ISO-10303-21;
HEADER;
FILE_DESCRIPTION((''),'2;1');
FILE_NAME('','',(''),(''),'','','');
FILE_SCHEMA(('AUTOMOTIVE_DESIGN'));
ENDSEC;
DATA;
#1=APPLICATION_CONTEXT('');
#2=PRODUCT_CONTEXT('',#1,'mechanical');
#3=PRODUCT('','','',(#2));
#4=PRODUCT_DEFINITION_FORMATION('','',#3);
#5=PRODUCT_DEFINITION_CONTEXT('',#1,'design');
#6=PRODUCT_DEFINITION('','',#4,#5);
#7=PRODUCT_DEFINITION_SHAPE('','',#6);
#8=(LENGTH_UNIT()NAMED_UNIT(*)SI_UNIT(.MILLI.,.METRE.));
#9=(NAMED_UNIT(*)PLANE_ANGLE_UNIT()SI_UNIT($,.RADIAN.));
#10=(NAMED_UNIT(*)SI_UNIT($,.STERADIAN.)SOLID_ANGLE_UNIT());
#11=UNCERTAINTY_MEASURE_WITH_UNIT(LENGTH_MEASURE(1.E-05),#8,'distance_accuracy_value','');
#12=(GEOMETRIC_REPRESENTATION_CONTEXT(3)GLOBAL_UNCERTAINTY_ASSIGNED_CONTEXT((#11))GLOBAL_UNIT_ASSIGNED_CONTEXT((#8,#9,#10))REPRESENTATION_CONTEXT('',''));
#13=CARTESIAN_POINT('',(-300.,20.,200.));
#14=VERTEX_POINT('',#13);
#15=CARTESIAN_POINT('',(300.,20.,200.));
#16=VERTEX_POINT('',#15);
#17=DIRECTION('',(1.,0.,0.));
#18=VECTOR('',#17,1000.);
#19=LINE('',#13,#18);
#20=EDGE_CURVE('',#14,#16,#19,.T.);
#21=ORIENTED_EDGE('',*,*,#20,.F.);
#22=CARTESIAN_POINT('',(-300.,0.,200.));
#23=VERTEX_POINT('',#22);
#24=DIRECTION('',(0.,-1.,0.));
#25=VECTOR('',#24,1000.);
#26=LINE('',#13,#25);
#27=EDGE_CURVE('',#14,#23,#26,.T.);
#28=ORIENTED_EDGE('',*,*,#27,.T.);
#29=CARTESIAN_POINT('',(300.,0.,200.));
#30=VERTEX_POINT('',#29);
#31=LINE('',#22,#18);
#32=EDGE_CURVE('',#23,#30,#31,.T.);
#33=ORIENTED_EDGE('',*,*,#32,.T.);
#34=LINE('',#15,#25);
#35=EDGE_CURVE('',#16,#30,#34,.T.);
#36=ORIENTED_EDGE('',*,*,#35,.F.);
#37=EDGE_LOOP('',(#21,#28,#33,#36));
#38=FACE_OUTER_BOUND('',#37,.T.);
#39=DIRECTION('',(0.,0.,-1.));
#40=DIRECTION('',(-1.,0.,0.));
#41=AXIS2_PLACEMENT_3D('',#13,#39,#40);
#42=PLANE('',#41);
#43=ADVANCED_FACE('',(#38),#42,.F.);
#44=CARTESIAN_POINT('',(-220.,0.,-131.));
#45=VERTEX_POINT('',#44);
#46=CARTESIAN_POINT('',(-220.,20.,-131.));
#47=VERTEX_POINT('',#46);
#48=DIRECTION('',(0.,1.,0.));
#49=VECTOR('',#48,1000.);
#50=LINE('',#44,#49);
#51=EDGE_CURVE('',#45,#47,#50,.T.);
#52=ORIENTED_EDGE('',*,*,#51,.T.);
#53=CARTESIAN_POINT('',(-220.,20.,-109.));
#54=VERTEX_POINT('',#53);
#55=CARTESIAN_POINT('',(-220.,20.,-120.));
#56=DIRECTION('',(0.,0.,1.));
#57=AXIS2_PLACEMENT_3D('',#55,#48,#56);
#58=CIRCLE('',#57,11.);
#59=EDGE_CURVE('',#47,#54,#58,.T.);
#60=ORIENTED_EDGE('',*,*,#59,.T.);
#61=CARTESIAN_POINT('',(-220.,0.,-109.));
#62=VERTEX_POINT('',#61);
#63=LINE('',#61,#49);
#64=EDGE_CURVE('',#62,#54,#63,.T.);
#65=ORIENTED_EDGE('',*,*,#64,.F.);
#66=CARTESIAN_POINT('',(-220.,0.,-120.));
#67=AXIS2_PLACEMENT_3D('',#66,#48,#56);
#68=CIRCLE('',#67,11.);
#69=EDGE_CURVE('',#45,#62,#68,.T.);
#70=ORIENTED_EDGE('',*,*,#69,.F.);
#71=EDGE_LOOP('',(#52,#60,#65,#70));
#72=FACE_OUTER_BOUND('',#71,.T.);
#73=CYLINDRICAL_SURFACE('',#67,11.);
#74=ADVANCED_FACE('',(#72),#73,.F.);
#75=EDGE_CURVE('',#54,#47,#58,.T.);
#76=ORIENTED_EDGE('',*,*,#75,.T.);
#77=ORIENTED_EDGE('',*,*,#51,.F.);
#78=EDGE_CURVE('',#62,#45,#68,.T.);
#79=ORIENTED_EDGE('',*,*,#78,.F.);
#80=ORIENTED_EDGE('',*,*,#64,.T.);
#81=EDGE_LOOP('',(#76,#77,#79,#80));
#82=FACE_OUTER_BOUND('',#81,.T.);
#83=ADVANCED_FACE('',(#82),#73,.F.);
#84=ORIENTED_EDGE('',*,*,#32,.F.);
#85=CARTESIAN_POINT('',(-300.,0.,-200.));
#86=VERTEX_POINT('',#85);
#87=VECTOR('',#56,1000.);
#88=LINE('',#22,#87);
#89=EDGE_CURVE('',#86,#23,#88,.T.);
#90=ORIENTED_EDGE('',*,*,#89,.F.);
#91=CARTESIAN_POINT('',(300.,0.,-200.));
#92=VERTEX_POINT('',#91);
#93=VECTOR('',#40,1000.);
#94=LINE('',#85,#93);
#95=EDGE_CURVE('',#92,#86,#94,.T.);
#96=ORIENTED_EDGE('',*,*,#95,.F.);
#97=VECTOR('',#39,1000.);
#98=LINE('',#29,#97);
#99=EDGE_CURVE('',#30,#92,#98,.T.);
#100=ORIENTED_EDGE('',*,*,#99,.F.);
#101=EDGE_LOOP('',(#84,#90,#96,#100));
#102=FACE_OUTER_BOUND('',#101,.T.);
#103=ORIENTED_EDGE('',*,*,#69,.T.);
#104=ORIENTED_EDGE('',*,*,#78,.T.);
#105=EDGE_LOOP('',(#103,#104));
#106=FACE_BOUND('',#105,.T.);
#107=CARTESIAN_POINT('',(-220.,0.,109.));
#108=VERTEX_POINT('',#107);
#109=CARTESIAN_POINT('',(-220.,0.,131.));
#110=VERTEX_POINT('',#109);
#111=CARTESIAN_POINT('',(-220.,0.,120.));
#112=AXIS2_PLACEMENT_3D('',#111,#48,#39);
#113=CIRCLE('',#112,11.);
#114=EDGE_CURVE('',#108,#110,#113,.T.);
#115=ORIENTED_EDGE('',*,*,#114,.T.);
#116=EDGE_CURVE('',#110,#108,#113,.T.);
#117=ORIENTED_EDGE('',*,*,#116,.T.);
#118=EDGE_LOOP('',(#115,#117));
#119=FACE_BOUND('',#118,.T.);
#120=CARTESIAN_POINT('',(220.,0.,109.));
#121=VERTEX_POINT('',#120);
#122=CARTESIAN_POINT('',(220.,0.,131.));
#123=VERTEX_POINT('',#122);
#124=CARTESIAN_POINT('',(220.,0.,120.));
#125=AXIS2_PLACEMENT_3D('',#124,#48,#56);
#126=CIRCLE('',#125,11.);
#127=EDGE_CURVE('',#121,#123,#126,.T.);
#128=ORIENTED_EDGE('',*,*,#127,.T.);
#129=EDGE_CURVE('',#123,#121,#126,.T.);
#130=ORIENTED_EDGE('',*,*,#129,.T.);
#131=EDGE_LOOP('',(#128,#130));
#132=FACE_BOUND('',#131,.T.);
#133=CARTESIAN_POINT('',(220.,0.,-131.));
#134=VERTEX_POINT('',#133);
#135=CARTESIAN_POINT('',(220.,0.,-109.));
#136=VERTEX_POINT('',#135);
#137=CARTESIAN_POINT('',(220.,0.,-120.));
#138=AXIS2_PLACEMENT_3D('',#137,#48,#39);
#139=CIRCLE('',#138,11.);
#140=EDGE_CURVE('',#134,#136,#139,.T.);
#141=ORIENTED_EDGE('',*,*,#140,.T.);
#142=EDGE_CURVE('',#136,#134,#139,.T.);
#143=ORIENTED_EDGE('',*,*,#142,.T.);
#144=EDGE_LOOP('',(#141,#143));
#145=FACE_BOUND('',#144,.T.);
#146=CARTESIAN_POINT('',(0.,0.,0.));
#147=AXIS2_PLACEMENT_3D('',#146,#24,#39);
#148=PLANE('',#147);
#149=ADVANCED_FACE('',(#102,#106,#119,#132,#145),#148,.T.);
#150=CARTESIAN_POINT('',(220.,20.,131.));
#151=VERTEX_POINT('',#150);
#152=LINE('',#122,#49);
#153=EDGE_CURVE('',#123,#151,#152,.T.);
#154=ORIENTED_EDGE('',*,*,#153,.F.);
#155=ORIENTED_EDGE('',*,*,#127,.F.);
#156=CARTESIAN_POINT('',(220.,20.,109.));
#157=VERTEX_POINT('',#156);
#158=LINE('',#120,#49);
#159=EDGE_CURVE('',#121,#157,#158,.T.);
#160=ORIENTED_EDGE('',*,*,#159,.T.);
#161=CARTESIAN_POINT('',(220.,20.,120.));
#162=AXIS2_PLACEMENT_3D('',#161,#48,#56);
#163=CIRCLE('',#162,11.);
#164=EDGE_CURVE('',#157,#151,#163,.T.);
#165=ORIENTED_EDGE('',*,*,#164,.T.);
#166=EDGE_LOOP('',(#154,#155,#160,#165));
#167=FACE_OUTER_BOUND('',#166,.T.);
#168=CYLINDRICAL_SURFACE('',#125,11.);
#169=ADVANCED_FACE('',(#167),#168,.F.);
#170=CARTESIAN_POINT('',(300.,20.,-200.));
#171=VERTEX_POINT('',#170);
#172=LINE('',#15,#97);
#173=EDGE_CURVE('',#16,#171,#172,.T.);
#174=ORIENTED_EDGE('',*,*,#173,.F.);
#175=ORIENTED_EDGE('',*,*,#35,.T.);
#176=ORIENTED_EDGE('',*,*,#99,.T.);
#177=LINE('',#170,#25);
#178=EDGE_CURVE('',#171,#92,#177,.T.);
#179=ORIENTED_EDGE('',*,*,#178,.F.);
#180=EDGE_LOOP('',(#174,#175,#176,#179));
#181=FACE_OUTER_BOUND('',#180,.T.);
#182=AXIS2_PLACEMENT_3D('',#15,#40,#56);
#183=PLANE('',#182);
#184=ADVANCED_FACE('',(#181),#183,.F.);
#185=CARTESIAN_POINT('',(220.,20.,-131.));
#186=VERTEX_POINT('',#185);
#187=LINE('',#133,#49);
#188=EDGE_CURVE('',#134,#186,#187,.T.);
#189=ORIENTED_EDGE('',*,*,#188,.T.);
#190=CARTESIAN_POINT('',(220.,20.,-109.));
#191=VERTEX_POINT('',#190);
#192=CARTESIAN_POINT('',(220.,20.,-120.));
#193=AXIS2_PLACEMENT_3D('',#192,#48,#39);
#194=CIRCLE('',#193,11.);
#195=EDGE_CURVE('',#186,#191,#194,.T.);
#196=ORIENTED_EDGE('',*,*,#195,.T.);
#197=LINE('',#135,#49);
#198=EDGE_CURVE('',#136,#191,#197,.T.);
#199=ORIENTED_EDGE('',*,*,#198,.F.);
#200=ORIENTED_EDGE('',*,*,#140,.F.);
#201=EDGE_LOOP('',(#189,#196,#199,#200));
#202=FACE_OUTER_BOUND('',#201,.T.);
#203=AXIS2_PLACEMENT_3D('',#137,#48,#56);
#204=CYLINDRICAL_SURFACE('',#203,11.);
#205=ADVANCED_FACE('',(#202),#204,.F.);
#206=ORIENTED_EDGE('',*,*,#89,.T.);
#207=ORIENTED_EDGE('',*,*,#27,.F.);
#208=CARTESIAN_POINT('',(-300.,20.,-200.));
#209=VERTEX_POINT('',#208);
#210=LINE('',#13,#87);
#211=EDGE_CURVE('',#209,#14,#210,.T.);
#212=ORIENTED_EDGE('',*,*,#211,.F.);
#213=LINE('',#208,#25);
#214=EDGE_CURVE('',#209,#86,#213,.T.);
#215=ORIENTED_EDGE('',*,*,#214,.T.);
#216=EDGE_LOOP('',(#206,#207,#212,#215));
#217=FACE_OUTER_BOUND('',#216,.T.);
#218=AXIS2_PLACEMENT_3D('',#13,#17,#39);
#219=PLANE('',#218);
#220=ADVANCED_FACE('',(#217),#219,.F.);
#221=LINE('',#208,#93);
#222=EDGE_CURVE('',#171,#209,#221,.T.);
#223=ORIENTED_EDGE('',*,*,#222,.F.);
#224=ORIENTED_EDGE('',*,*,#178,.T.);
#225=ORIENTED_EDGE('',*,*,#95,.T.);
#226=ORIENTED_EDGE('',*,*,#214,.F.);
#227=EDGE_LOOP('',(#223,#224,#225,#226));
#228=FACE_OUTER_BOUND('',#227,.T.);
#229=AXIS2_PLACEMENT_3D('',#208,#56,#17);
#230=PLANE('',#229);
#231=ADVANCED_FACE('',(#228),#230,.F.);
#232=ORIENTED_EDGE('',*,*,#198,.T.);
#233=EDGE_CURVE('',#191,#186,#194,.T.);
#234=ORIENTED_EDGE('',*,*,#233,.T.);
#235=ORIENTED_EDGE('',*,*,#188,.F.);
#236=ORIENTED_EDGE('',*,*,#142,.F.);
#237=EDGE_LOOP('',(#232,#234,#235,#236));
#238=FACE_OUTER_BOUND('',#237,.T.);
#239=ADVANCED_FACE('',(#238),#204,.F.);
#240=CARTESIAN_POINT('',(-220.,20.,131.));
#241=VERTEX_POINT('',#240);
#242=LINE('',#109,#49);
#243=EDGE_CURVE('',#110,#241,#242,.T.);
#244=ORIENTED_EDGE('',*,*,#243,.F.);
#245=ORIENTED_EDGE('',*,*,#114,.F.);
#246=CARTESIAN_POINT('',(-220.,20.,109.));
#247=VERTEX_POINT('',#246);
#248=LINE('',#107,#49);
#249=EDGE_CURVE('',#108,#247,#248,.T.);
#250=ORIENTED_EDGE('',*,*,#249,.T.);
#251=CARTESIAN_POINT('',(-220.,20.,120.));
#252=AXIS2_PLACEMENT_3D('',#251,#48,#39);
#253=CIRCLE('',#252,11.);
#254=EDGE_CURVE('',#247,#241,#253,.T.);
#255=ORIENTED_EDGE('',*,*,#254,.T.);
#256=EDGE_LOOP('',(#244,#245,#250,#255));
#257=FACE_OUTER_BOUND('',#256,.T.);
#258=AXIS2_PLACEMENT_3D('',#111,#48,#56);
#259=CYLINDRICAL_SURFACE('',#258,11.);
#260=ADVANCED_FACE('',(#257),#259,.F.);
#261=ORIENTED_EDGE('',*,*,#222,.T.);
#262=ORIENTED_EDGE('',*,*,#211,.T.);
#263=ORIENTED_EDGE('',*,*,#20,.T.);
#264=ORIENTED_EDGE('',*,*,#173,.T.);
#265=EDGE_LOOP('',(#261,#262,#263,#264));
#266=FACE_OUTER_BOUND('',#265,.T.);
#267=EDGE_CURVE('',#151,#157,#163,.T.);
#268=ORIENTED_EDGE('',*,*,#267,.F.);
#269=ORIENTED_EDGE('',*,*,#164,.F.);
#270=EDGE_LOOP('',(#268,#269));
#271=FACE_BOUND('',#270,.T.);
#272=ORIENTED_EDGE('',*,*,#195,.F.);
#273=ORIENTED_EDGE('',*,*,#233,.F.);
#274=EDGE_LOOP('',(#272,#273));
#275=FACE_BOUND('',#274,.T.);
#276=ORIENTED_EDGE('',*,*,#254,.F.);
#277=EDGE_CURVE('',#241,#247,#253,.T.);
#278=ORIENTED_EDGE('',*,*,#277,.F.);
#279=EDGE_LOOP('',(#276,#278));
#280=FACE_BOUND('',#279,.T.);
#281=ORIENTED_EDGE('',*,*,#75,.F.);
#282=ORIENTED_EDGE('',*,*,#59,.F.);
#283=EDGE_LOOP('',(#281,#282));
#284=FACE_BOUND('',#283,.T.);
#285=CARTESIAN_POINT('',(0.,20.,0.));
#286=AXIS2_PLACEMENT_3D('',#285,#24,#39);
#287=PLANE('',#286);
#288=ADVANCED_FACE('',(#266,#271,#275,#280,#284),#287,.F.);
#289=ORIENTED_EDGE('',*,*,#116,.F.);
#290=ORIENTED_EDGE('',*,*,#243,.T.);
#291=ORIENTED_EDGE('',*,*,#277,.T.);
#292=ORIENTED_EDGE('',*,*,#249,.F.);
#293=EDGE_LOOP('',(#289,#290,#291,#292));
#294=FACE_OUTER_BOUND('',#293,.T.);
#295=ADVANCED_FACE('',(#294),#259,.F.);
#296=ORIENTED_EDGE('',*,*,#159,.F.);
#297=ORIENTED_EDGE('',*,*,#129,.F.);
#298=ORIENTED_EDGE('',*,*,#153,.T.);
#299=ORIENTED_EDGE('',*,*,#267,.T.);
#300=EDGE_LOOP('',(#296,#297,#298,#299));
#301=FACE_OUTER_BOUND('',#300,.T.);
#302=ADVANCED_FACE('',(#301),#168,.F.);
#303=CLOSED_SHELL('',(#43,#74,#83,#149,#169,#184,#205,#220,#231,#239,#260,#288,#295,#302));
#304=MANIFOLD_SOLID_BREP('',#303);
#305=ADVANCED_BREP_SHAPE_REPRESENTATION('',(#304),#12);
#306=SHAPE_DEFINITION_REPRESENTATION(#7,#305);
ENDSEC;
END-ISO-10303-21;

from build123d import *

# Parameters (mm, degrees)
SKETCH1_W           = 600
SKETCH1_H           = 400
BOSS_EXTRUDE1_DEPTH = 20
SKETCH2_R           = 11
CUT_EXTRUDE1_DEPTH  = 20


with BuildPart() as part:
    # Sketch1 → Boss-Extrude1 (new body)
    with BuildSketch(Plane(origin=(0, 0, 0), x_dir=(1, 0, 0), z_dir=(0, 1, 0))):
        Rectangle(SKETCH1_W, SKETCH1_H)
    extrude(amount=BOSS_EXTRUDE1_DEPTH)

    # Sketch2 → Cut-Extrude1 (cut)
    with BuildSketch(Plane(origin=(0, 20, 0), x_dir=(1, 0, 0), z_dir=(0, 1, 0))):
        with Locations(Location((-220, 120, 0), (0, 0, 270))):
            Circle(SKETCH2_R)
        with Locations(Location((220, 120, 0), (0, 0, 90))):
            Circle(SKETCH2_R)
        with Locations(Location((220, -120, 0), (0, 0, 270))):
            Circle(SKETCH2_R)
        with Locations(Location((-220, -120, 0), (0, 0, 90))):
            Circle(SKETCH2_R)
    extrude(amount=-CUT_EXTRUDE1_DEPTH, mode=Mode.SUBTRACT)


solid = part.part
